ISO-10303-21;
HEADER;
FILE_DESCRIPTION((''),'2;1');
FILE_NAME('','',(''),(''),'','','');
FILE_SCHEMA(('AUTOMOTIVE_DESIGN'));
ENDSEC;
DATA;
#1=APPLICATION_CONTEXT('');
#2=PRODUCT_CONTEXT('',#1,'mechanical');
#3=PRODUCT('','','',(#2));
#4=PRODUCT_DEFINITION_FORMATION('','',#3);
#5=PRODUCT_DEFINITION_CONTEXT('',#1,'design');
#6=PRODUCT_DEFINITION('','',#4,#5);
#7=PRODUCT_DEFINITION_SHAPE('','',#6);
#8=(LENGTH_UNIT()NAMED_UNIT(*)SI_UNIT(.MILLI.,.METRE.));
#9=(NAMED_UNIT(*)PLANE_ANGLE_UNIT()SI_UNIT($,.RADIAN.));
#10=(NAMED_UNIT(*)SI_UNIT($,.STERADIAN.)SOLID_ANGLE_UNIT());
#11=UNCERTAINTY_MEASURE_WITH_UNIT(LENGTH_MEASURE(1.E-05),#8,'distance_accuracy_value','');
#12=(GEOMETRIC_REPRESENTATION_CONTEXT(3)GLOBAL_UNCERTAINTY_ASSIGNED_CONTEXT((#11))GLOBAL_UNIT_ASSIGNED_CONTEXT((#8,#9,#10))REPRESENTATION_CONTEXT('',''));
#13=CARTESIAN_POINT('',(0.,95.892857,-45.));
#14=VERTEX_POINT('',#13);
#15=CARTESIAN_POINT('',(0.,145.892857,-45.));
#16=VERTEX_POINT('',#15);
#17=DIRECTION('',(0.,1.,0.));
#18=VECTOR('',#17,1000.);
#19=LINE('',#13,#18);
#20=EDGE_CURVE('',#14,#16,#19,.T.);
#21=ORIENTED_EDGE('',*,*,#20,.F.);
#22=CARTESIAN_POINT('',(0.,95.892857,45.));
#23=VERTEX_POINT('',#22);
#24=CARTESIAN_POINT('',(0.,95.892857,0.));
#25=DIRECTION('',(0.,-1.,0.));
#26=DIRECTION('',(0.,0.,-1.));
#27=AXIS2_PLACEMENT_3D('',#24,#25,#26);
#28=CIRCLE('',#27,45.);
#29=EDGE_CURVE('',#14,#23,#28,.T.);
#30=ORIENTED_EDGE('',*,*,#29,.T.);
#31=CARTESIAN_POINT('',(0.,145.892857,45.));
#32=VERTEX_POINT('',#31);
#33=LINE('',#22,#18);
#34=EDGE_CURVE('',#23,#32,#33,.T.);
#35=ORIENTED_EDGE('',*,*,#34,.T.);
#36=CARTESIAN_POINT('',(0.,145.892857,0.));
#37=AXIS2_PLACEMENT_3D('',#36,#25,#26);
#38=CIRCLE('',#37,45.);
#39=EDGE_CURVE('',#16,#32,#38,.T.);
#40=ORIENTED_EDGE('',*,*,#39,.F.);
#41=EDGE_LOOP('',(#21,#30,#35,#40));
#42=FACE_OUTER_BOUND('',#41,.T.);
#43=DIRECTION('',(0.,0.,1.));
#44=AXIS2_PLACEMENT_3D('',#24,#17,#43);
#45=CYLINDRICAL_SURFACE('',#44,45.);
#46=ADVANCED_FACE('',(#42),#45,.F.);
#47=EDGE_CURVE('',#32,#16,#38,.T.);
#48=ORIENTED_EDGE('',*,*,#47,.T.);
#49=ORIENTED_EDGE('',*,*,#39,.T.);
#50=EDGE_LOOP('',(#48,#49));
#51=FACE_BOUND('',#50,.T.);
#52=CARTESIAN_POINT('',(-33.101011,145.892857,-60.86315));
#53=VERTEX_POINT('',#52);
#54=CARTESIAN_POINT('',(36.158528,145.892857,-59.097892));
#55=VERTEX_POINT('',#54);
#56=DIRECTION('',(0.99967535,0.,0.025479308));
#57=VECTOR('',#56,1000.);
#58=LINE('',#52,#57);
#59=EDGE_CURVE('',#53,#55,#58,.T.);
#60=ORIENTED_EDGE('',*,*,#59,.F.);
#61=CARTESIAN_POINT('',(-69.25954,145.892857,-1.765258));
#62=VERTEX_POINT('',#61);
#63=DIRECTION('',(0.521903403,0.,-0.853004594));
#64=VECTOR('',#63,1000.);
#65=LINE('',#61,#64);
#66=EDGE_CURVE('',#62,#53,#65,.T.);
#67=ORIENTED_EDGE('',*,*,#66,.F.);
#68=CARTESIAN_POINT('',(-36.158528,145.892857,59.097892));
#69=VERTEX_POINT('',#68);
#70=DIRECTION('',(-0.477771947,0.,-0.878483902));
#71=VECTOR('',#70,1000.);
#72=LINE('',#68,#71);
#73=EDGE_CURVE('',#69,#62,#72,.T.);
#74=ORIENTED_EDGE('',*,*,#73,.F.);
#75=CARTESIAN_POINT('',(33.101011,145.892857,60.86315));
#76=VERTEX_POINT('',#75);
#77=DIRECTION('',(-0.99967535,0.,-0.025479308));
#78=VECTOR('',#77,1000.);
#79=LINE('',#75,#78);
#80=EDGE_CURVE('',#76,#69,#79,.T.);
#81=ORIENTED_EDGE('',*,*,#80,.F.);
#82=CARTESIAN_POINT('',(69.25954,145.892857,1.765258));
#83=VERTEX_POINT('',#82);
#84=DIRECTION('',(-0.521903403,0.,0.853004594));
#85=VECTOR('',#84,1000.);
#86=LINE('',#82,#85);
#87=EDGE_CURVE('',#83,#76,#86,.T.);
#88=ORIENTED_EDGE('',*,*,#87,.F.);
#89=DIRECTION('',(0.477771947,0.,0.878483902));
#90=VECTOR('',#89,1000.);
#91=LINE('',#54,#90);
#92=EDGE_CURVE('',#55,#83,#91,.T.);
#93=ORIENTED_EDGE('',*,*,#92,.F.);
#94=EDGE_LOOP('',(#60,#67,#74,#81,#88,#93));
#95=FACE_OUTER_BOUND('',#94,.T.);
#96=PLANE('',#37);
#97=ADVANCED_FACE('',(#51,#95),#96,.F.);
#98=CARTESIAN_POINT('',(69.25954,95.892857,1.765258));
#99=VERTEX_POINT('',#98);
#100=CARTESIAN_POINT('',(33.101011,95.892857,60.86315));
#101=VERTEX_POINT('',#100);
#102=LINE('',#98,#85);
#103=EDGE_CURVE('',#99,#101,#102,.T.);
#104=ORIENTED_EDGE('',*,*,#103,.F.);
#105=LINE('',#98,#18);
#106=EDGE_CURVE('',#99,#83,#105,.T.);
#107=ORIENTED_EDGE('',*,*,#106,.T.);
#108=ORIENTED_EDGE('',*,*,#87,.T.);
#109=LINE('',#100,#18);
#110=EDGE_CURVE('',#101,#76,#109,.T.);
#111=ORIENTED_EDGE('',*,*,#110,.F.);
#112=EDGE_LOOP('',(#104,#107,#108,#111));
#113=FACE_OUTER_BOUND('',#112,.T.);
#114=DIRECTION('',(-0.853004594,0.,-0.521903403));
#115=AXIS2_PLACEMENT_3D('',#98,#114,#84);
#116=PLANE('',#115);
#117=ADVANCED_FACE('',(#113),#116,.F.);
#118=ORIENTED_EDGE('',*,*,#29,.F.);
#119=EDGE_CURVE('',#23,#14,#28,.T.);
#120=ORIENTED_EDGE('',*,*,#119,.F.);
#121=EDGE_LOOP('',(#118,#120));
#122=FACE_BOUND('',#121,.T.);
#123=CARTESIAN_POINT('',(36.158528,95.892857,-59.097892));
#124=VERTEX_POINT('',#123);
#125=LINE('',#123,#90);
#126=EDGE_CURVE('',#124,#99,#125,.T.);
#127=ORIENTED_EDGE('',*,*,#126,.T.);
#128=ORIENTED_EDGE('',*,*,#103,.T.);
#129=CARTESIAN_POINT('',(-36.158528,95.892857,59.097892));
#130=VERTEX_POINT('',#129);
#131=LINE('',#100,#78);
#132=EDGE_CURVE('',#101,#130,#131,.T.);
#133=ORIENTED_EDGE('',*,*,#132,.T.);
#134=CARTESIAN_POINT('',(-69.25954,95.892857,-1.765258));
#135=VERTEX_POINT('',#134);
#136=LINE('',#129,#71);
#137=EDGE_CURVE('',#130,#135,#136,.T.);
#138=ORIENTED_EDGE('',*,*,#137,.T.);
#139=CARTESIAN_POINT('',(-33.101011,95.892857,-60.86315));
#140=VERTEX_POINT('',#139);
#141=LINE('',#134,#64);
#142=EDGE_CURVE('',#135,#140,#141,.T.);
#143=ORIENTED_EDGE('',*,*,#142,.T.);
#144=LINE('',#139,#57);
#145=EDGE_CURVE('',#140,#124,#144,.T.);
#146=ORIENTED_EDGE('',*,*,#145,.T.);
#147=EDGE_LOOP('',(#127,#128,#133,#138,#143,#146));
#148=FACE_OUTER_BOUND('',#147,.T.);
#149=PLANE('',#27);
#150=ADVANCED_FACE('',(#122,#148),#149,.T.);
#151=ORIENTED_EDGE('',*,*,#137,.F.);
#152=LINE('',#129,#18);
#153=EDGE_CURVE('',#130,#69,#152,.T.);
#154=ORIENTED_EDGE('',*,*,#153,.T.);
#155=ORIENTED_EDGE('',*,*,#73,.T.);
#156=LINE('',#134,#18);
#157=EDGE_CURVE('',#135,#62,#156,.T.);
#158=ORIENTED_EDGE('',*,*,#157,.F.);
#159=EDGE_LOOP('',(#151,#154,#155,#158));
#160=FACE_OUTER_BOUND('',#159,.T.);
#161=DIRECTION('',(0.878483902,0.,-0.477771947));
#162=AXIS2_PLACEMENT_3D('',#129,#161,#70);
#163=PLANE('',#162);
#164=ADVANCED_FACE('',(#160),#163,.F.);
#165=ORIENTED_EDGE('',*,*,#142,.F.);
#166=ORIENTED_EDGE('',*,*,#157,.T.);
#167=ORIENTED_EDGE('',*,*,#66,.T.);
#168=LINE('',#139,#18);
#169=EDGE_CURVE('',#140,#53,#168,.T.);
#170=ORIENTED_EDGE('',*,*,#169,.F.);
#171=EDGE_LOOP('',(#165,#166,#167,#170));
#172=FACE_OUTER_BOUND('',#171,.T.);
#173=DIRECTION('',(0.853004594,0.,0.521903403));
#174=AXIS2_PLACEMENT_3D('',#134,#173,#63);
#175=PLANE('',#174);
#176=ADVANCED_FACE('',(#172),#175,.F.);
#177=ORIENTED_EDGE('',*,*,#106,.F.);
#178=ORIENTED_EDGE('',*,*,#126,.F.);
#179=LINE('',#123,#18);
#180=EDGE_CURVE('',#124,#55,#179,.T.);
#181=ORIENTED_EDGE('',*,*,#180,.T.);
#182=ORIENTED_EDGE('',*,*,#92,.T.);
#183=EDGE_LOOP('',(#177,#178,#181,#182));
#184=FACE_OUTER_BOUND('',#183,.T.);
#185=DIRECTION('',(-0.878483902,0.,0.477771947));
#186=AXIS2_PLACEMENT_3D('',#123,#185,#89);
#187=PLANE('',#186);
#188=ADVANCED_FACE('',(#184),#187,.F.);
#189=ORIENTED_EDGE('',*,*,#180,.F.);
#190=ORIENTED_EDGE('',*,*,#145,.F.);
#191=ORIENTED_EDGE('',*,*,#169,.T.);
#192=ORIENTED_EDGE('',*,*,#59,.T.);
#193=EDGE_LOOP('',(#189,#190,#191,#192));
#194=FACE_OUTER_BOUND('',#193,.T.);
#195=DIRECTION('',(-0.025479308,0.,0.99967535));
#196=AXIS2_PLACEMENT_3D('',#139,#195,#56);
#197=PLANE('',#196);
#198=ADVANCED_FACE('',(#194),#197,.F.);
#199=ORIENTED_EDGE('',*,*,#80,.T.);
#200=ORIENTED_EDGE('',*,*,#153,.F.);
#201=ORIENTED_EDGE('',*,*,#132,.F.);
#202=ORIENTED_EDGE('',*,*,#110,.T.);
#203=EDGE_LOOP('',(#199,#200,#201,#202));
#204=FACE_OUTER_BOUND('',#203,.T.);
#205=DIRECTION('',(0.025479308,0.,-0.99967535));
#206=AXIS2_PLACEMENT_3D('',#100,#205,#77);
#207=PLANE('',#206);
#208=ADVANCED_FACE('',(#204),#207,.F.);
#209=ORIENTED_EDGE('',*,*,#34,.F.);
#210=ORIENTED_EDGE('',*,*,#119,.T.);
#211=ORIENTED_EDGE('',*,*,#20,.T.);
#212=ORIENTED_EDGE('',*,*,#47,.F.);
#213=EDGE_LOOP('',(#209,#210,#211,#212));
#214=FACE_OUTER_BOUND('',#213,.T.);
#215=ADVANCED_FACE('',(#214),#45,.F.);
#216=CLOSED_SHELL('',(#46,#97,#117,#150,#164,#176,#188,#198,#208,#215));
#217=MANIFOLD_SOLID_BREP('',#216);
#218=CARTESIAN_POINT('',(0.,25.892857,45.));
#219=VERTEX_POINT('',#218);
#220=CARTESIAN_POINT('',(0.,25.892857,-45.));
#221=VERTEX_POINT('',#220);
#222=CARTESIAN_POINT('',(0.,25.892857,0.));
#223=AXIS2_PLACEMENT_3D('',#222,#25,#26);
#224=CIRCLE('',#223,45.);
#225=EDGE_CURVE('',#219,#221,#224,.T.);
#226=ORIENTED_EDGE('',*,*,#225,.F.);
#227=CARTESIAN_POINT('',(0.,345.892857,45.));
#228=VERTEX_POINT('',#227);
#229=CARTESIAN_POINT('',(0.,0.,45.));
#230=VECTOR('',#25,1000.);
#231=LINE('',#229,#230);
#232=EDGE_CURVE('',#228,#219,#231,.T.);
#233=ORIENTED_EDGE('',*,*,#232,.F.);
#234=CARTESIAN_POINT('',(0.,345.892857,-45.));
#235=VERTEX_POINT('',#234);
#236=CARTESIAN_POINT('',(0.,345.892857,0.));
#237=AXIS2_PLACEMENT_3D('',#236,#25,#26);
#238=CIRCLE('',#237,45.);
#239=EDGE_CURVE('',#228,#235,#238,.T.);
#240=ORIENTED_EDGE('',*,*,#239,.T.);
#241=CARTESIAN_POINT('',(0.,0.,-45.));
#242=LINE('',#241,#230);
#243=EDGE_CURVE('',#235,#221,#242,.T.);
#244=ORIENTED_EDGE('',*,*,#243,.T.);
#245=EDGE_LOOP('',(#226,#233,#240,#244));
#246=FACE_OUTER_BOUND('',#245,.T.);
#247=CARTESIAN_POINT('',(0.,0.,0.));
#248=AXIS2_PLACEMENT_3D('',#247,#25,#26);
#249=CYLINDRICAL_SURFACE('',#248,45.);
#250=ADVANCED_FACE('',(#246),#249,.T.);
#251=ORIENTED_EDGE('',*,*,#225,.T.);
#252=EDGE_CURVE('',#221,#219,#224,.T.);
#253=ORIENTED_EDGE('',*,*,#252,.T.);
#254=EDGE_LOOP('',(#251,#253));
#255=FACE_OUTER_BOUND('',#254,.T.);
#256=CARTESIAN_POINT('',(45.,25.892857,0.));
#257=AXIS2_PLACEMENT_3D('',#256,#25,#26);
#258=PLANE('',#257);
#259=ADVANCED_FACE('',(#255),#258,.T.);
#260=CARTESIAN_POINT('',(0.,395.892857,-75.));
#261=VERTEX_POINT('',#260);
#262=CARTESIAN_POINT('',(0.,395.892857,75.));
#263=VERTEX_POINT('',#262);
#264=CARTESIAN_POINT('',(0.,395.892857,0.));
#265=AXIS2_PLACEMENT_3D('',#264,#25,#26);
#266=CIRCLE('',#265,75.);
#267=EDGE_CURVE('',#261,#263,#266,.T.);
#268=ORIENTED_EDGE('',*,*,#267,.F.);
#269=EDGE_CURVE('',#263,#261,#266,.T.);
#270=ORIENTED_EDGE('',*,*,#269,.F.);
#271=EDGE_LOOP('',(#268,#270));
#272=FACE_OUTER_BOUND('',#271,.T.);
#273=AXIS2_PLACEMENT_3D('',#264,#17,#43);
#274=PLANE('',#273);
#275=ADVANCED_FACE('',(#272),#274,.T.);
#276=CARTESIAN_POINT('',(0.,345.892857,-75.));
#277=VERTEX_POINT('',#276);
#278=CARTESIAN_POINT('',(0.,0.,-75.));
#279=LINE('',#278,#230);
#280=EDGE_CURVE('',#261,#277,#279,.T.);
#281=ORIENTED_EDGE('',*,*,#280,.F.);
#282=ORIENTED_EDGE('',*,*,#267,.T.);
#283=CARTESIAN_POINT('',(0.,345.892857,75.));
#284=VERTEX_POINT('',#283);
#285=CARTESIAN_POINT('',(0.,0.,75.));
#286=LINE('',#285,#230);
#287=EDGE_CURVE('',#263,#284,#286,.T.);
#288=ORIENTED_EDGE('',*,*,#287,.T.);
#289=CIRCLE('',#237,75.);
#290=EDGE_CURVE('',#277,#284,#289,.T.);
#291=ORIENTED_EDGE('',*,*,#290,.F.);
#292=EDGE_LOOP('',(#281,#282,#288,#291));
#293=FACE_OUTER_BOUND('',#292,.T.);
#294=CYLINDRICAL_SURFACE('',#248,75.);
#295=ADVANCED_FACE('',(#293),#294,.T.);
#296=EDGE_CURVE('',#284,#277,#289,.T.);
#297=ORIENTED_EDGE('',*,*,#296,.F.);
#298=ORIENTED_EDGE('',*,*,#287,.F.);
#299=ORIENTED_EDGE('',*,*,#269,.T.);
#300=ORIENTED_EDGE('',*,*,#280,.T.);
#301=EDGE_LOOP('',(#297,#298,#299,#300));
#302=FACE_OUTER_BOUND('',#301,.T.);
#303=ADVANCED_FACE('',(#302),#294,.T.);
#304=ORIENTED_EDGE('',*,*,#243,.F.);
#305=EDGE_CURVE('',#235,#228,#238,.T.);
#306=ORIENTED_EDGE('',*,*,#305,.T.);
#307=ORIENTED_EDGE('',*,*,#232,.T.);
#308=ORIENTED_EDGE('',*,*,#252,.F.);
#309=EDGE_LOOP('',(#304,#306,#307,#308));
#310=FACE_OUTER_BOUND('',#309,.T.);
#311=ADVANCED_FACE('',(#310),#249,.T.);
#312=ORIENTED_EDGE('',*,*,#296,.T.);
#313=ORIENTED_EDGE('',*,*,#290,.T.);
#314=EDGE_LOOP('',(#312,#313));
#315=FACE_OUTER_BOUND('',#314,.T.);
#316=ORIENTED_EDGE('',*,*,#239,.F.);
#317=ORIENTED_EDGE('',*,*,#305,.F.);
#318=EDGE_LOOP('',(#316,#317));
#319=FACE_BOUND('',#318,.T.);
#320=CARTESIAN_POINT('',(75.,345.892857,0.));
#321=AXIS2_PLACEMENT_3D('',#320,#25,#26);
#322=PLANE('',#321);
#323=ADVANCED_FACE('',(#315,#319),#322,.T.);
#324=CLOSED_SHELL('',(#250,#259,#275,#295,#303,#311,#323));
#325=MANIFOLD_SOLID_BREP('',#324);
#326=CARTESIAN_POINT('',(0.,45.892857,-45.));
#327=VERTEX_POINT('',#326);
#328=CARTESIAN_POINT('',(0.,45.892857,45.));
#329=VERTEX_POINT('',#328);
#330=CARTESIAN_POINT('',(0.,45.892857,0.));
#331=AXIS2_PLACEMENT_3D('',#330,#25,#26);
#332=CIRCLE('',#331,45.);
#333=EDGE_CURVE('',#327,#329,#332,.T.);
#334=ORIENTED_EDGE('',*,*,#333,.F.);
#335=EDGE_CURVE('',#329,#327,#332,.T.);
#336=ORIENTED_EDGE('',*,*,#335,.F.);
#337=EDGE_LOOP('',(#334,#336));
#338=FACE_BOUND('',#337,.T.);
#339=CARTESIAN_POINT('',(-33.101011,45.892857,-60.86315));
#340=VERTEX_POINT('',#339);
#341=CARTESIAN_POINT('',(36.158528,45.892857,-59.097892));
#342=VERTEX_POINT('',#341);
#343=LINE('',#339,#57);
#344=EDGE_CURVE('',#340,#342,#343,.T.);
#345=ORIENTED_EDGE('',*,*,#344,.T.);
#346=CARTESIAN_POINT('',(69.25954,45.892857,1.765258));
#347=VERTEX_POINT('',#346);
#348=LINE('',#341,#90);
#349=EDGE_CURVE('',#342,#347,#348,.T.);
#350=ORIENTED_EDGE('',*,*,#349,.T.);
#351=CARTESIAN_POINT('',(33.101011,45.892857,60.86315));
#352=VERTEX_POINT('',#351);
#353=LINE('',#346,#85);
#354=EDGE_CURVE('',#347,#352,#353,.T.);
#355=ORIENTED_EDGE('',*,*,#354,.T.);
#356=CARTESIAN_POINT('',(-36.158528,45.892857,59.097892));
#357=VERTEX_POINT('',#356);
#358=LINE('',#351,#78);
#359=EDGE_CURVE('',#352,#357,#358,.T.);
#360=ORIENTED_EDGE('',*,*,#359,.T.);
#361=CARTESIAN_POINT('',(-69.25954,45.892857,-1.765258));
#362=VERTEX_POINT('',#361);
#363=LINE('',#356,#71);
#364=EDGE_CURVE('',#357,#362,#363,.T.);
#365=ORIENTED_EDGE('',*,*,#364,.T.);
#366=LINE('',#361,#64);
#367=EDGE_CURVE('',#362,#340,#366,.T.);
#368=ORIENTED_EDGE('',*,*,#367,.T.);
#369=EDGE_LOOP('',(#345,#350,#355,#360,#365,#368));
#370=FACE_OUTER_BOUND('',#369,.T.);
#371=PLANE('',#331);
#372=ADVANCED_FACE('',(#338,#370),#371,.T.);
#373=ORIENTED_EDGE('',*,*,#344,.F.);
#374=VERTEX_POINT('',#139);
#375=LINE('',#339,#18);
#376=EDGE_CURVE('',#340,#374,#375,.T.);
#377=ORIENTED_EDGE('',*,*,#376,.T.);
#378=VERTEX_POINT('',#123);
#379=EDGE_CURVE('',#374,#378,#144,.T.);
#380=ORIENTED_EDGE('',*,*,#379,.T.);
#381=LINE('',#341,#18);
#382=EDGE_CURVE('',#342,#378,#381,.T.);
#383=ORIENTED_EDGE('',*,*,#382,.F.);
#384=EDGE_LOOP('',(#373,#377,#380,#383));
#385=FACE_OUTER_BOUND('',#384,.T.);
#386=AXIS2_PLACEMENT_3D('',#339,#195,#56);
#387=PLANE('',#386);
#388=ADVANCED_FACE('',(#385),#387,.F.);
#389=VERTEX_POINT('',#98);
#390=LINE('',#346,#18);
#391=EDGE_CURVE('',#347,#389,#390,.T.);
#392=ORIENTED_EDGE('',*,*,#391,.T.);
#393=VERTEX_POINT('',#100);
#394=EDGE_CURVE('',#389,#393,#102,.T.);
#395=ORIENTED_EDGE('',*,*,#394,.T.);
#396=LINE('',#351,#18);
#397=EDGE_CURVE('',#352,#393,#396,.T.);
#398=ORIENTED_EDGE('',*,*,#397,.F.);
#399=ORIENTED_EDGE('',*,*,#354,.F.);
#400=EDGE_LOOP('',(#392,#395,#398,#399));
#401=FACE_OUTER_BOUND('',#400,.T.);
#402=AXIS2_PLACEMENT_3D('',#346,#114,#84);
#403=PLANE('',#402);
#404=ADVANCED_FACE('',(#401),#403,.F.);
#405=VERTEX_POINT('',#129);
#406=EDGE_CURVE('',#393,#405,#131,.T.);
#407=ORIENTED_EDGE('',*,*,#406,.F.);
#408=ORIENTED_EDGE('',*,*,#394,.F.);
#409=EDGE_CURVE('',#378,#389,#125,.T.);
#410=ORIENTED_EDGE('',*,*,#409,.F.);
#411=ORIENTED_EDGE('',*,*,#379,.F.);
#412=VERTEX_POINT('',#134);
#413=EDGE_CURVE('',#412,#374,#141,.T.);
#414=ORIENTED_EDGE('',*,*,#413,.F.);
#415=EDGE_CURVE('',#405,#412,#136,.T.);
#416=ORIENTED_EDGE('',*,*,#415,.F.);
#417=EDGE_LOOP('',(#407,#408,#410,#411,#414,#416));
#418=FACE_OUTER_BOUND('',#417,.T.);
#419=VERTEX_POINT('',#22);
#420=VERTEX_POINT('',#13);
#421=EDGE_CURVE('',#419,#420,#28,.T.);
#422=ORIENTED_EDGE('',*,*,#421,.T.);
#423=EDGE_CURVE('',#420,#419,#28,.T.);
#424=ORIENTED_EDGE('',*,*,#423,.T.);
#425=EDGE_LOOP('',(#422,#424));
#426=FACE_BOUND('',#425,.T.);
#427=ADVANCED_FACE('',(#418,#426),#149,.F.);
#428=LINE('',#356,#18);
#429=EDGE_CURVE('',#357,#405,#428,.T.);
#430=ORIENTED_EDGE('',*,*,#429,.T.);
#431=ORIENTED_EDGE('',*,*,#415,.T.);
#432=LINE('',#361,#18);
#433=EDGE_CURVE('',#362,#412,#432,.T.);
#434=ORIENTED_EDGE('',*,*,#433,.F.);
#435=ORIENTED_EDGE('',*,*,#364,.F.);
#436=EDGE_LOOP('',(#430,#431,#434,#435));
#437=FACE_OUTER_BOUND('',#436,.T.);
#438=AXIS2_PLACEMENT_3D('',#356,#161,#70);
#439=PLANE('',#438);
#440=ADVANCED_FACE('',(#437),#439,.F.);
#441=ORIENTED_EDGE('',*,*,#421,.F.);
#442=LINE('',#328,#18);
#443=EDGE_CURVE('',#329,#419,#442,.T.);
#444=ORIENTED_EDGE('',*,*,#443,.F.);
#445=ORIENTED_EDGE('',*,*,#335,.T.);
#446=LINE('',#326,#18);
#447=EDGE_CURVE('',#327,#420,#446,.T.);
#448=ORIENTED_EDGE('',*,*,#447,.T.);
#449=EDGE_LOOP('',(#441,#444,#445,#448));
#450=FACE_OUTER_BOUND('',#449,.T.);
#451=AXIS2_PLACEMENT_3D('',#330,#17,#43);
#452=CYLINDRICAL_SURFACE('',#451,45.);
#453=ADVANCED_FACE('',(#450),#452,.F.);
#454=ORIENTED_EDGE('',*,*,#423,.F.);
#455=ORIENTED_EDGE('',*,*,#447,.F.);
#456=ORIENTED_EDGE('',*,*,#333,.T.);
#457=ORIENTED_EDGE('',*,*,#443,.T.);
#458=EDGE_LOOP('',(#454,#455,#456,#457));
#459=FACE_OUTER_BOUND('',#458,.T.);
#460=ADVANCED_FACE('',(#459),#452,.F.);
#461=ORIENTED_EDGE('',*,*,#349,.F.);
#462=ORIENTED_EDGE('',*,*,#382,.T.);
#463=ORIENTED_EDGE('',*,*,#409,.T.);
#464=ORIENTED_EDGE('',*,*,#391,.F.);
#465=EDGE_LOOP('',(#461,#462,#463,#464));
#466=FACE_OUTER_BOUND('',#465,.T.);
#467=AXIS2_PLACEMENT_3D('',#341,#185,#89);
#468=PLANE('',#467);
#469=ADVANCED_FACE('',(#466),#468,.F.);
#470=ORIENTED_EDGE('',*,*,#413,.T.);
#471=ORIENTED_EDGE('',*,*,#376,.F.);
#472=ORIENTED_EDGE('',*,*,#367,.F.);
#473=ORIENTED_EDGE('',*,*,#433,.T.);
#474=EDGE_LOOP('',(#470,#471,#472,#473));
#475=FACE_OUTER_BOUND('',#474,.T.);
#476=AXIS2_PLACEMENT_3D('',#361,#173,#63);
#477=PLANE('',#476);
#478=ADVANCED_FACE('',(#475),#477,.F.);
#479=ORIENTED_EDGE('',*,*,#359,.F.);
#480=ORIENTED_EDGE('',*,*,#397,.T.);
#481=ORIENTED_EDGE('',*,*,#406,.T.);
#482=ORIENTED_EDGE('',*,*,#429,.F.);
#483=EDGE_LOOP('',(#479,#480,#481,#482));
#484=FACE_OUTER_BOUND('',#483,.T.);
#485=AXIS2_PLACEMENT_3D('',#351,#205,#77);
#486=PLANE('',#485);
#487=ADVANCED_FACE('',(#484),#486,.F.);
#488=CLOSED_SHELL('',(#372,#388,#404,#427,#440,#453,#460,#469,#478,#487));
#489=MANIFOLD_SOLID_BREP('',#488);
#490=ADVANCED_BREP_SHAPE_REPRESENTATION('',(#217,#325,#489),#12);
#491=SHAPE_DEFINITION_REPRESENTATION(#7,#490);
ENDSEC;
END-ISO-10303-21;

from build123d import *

# Parameters (mm, degrees)
SKETCH2_R           = 45
BOSS_EXTRUDE1_DEPTH = 50
LPATTERN1_COUNT     = 2
LPATTERN1_PITCH     = 50


with BuildPart() as part:
    # Sketch1 → Revolve1 (revolve)
    with BuildSketch(Plane.XY, mode=Mode.PRIVATE) as revolve1_sk:
        Polygon((0, 395.892857143), (75, 395.892857143), (75, 345.892857143), (45, 345.892857143), (45, 25.892857143), (0, 25.892857143), align=None)
    revolve(revolve1_sk.sketch.rotate(Axis((0, 0, 0), (0, 1, 0)), 90), axis=Axis((0, 0, 0), (0, 1, 0)))


with BuildPart() as body_2:
    # Sketch2 → Boss-Extrude1 (new body)
    with BuildSketch(Plane(origin=(0, 145.892857143, 0), x_dir=(-1, 0, 0), z_dir=(0, -1, 0))):
        Polygon((-33.101011459, -60.863150102), (36.158528413, -59.097891866), (69.259539873, 1.765258237), (33.101011459, 60.863150102), (-36.158528413, 59.097891866), (-69.259539873, -1.765258237), align=None)
        with Locations(Location((0, 0, 0), (0, 0, 90))):
            Circle(SKETCH2_R, mode=Mode.SUBTRACT)
    extrude(amount=BOSS_EXTRUDE1_DEPTH)


with BuildPart() as lpattern1_1:
    # LPattern1: pattern copy
    add(body_2.part.moved(Location(Vector(0, -1, 0) * (1 * LPATTERN1_PITCH))))


solid = Compound([part.part, body_2.part, lpattern1_1.part])
